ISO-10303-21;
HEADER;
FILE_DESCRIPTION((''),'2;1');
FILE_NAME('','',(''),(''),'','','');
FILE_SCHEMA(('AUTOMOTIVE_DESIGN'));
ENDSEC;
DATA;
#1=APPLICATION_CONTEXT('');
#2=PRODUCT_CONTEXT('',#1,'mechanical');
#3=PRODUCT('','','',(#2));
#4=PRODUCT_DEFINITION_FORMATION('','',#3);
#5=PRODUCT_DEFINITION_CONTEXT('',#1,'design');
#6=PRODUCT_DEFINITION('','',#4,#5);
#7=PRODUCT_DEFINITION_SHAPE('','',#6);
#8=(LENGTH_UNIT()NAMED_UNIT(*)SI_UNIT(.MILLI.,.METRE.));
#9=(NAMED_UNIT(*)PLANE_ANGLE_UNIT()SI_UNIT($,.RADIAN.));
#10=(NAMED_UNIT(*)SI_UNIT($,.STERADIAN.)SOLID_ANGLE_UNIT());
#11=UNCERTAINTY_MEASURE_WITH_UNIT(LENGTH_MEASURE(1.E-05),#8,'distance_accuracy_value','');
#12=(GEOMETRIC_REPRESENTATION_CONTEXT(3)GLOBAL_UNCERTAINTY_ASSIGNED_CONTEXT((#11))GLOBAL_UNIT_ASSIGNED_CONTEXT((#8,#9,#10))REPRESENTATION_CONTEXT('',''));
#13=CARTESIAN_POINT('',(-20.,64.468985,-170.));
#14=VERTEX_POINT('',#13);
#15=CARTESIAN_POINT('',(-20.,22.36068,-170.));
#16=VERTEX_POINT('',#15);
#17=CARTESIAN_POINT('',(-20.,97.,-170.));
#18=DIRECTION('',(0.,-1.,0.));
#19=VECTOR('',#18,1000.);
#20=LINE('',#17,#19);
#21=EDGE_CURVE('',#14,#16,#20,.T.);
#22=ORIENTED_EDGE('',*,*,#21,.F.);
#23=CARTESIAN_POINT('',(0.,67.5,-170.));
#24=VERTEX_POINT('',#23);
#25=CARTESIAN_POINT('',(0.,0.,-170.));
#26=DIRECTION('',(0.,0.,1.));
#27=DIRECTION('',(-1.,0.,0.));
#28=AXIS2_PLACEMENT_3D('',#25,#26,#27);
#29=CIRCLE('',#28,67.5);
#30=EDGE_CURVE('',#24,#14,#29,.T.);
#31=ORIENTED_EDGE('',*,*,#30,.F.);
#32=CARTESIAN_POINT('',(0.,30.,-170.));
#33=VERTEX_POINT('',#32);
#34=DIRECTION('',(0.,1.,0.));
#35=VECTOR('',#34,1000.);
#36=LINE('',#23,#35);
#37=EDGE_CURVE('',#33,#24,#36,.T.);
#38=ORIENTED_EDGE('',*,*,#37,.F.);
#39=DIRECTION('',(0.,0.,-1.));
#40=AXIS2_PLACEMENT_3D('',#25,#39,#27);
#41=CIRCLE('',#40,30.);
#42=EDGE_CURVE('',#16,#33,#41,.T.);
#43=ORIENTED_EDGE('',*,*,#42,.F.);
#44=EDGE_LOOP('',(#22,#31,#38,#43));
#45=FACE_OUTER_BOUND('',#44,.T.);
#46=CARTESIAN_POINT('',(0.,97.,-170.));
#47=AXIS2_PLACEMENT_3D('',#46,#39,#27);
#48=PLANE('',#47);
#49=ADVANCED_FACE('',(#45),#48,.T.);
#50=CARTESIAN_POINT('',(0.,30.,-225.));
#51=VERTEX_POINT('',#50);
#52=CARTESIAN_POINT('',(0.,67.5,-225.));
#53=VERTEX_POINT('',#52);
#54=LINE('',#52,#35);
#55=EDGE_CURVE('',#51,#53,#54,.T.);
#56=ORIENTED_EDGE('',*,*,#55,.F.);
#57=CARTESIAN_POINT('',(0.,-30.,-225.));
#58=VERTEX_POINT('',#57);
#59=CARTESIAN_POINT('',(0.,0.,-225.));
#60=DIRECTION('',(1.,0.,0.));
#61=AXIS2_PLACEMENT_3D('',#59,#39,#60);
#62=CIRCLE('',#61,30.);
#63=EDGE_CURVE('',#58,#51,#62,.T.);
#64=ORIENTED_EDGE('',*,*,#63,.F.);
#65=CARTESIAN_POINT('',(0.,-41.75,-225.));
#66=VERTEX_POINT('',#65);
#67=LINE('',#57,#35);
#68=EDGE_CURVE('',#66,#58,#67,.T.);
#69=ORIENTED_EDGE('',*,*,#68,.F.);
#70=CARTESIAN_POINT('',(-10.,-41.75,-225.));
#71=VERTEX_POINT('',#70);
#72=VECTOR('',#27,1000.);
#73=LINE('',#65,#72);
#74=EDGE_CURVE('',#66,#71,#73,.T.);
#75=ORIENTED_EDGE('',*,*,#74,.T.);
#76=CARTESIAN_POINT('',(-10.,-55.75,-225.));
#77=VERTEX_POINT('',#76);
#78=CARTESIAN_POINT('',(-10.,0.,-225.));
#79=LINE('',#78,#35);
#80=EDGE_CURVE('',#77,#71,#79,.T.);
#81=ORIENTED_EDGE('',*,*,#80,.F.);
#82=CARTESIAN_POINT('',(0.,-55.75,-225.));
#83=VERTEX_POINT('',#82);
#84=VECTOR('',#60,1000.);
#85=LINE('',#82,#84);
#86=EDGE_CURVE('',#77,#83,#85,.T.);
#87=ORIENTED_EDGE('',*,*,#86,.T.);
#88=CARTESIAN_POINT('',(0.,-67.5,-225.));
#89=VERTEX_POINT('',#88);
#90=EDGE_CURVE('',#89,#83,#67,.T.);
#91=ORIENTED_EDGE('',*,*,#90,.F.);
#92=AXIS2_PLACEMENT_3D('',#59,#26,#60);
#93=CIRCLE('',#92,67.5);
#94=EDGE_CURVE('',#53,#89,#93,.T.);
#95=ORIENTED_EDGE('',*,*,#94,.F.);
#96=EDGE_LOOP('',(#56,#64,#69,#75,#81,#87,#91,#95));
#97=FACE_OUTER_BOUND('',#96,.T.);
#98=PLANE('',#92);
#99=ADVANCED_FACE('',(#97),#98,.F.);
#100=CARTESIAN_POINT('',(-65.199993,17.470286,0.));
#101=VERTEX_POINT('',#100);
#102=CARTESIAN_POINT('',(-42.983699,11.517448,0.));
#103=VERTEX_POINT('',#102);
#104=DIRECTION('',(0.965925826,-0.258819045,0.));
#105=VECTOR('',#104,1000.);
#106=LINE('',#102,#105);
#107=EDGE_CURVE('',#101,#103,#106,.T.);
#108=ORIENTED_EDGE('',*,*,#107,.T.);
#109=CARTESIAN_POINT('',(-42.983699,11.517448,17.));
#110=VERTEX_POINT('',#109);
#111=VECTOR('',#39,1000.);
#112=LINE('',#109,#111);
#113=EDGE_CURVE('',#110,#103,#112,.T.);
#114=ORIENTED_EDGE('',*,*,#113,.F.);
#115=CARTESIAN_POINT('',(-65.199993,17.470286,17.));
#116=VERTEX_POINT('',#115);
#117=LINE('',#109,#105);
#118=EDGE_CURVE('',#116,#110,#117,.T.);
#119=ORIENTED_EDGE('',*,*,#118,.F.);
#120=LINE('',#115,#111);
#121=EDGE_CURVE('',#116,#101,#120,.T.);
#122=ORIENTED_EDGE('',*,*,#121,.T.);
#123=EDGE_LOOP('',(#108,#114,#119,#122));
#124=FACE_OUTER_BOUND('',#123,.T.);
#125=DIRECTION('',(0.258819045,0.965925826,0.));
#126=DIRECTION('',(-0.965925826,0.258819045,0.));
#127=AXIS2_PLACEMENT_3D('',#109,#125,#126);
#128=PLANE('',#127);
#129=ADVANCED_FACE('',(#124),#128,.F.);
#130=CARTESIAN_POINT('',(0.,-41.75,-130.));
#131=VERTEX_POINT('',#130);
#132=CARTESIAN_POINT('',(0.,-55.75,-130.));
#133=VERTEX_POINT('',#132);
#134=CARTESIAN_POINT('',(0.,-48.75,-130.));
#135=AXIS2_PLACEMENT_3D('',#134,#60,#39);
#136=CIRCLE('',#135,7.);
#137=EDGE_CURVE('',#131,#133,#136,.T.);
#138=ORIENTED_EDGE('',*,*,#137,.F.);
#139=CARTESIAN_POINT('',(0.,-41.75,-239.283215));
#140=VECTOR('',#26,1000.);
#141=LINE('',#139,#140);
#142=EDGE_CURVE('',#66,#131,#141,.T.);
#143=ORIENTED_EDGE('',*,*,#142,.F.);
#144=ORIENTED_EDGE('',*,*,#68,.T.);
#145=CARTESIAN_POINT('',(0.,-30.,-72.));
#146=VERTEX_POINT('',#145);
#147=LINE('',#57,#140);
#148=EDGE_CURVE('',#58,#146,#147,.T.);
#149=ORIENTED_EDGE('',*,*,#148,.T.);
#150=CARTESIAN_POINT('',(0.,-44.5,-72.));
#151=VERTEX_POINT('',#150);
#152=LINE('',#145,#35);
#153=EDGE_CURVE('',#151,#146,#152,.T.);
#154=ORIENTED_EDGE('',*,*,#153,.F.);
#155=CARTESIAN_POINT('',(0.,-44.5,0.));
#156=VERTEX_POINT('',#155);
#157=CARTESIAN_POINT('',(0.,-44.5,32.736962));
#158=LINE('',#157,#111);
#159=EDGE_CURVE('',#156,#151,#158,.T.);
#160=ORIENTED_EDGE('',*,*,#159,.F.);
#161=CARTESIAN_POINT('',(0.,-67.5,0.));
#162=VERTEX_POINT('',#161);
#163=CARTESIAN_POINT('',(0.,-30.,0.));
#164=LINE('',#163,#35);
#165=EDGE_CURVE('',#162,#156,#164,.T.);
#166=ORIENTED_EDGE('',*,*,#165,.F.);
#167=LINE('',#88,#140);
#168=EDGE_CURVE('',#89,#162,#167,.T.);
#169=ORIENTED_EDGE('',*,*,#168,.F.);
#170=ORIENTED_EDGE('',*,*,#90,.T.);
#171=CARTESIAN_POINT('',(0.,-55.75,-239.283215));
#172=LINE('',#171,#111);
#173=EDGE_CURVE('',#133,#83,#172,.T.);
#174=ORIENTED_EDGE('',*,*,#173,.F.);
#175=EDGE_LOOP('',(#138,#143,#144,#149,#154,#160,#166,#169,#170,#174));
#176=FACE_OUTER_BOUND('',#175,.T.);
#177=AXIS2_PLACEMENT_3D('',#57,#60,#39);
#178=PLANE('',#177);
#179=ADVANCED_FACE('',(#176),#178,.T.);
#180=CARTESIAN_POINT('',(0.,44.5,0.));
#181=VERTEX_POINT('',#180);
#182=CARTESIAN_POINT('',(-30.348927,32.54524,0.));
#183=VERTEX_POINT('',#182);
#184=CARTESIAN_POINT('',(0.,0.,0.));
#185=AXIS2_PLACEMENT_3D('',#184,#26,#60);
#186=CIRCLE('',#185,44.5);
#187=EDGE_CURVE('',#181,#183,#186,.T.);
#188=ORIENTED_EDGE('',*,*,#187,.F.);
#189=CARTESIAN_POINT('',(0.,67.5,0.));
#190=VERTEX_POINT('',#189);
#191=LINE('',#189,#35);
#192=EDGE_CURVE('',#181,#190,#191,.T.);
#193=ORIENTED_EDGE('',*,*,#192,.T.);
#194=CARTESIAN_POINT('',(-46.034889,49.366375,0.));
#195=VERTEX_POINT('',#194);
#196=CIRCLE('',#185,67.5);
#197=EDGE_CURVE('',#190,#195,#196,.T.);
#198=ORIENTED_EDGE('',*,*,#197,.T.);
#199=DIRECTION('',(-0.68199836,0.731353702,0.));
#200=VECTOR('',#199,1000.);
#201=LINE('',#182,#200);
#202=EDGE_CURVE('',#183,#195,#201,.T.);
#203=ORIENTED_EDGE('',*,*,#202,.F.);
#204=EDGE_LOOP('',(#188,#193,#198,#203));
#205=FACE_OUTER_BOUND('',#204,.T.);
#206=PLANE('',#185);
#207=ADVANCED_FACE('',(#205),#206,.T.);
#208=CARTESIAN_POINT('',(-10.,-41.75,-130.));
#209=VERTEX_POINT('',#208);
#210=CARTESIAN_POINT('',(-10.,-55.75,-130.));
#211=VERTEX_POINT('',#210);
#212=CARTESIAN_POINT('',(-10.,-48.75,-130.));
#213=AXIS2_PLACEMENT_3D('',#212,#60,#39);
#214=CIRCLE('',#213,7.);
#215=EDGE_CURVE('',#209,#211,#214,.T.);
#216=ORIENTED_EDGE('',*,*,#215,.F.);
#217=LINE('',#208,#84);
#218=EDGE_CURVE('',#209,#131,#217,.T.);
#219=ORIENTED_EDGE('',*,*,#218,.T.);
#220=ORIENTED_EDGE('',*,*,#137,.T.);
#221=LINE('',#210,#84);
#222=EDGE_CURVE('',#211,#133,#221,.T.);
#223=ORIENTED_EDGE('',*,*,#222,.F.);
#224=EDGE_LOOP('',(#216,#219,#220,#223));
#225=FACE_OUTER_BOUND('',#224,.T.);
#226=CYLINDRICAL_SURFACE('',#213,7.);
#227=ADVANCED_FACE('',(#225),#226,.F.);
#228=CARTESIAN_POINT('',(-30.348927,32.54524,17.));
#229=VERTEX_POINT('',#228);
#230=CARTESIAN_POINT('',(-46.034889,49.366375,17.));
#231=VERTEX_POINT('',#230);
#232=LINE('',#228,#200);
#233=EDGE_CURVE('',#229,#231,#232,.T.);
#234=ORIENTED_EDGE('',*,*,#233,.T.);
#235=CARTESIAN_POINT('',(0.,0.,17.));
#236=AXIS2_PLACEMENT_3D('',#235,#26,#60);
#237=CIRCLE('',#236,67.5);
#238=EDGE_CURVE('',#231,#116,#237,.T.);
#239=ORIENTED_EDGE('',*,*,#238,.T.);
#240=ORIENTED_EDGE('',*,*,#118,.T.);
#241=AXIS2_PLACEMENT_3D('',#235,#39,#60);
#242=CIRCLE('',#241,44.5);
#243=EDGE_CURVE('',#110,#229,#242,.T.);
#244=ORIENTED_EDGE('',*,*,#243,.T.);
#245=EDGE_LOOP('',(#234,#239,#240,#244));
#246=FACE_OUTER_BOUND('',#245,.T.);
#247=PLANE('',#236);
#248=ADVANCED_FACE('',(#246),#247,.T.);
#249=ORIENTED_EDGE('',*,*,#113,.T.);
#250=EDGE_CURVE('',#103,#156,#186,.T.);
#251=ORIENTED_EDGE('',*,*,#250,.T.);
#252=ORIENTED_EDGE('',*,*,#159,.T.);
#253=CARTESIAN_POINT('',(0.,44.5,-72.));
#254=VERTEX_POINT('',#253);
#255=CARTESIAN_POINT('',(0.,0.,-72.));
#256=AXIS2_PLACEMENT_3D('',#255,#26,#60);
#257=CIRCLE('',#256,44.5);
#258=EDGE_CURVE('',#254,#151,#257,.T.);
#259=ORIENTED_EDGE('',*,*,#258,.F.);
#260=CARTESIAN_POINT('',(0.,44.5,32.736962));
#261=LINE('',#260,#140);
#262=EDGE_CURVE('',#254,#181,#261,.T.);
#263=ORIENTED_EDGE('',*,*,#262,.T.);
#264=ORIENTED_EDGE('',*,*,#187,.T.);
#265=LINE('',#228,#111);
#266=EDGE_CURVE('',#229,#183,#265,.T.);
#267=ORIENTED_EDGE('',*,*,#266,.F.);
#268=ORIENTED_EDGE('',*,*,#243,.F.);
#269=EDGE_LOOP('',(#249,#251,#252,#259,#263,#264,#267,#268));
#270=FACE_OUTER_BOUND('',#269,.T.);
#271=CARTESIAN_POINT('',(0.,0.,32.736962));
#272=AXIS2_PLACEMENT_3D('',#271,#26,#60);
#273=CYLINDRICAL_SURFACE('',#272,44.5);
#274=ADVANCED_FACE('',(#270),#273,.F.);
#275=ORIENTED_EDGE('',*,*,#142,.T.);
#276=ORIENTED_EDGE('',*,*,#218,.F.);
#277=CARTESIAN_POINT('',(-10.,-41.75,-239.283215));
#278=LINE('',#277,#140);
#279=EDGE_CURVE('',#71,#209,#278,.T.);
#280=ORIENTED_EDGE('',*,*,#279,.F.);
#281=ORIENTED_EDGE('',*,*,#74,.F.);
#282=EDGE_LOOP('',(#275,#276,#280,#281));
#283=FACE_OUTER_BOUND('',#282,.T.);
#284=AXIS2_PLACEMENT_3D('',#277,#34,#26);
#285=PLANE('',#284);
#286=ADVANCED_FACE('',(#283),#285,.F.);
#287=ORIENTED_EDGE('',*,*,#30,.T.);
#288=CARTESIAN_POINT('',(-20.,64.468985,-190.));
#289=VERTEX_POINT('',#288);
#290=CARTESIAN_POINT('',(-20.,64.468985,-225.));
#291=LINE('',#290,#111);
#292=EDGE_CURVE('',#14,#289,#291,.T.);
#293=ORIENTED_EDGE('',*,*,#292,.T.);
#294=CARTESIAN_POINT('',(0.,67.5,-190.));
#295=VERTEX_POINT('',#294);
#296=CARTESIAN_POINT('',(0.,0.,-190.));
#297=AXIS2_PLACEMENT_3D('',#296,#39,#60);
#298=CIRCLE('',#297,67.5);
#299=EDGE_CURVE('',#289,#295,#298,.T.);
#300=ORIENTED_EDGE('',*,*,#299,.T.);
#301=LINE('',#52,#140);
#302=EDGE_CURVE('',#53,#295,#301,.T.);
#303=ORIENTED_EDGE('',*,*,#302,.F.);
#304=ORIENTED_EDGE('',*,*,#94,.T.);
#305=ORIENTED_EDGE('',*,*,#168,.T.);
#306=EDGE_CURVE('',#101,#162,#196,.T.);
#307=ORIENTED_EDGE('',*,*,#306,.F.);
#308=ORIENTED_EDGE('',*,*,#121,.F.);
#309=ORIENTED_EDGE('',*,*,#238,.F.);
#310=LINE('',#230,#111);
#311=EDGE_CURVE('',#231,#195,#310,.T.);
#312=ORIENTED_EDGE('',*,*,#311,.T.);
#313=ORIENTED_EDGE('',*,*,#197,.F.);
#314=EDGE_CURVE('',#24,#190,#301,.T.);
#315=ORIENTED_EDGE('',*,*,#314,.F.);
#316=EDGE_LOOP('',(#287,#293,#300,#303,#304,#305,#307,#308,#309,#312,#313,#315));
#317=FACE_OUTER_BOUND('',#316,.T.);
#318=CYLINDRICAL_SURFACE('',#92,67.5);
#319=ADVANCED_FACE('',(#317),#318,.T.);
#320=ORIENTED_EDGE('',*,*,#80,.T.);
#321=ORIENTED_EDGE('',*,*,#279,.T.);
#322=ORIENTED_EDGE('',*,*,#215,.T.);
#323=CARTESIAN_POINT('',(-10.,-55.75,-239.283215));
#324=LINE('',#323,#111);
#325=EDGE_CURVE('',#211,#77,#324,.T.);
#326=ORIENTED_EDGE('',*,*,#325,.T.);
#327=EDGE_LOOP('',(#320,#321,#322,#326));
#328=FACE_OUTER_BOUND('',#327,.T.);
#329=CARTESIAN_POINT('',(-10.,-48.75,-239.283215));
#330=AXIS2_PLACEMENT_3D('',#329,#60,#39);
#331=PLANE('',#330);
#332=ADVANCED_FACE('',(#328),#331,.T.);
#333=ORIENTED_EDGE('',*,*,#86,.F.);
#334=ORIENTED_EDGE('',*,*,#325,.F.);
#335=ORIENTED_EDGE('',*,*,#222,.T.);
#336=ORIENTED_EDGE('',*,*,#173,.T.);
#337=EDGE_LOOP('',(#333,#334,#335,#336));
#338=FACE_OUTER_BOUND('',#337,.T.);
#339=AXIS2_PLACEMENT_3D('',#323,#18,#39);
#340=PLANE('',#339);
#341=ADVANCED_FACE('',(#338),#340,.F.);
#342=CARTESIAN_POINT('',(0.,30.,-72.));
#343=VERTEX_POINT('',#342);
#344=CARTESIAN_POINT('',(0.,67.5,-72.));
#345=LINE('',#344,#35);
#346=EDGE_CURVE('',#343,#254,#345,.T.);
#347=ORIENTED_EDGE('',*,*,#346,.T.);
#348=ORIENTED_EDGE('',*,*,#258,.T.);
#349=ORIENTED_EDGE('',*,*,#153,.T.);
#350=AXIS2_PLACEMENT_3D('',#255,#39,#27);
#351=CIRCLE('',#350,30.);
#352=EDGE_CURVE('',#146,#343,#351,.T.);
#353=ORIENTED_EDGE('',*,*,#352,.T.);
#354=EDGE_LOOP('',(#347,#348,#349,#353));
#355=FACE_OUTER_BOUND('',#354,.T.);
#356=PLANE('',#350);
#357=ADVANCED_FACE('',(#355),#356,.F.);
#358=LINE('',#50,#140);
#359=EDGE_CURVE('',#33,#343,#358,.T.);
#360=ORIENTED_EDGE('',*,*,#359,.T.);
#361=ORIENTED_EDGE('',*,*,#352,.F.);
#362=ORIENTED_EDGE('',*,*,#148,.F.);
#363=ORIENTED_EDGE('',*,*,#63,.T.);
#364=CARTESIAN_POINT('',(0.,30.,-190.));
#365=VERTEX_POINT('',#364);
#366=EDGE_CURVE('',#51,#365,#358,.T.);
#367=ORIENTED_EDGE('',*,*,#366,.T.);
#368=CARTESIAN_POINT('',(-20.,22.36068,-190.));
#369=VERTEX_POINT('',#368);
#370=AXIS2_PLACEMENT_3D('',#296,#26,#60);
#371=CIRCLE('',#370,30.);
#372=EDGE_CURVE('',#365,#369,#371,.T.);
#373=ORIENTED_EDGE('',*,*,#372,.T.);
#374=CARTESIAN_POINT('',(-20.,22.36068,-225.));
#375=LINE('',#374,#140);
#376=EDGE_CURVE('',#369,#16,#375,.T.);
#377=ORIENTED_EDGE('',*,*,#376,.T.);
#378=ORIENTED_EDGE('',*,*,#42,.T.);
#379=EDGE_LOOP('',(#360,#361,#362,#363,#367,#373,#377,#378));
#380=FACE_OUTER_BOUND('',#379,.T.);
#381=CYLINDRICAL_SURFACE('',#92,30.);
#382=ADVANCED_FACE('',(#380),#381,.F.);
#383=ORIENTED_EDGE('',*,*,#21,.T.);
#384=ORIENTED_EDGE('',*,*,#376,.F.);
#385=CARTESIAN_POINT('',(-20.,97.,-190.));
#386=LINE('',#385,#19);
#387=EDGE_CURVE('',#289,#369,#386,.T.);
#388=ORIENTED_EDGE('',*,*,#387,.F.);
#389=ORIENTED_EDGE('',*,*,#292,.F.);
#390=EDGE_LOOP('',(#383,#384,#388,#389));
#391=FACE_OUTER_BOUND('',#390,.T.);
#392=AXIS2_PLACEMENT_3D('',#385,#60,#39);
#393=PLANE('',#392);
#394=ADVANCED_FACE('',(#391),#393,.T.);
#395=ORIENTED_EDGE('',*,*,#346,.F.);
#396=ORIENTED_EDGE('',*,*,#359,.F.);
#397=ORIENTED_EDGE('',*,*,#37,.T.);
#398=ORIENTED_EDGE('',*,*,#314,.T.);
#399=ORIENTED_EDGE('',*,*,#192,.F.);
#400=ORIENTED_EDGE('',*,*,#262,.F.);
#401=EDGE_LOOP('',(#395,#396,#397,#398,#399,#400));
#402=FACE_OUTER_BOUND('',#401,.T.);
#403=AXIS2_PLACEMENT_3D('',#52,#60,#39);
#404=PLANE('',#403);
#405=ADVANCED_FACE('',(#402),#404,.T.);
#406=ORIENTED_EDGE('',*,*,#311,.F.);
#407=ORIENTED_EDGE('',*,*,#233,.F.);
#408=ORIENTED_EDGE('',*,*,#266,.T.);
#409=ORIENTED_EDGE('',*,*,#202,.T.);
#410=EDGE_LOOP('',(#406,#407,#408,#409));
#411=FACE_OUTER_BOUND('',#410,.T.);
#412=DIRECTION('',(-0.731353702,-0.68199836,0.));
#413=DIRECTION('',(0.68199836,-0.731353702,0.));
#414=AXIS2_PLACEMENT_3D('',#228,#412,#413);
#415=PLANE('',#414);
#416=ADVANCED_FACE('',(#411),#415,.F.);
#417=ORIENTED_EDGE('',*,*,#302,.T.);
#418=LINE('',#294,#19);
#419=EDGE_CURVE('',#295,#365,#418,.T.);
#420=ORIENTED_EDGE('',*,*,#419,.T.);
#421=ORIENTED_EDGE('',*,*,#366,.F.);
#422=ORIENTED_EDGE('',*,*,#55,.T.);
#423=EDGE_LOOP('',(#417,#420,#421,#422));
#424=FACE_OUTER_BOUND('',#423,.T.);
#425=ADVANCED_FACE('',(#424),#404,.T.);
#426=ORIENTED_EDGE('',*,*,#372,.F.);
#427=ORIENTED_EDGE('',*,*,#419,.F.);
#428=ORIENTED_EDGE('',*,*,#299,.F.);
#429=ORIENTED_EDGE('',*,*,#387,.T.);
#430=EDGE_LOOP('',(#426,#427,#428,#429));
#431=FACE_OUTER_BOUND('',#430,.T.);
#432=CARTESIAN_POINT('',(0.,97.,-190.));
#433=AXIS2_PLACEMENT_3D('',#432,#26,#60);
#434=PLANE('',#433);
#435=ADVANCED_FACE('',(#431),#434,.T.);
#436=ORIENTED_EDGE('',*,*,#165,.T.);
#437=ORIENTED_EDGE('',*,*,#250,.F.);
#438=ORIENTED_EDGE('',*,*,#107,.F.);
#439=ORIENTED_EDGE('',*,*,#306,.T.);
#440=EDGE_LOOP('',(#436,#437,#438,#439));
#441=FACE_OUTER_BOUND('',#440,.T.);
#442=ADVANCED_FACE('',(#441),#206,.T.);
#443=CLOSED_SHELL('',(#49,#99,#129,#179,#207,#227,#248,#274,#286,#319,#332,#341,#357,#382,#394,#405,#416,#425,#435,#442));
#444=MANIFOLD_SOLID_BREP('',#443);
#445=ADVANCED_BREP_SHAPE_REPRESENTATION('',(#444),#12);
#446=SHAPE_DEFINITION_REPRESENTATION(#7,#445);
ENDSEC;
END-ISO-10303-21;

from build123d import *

# Parameters (mm, degrees)
BASE_BLOCK_60X135X225_DEPTH = 225
BORE_PROFILE_SKETCH_W       = 72
BORE_PROFILE_SKETCH_H       = 44.5
SECTOR_START                = 17
SECTOR_BOSS_32DEG_X17_DEPTH = 17
END_NOTCH_SKETCH_W          = 20
END_NOTCH_SKETCH_H          = 20
END_NOTCH_20X35_DEPTH       = 97
SLOT_7X95_DEPTH             = 10


with BuildPart() as part:
    # Base Block Sketch → Base Block 60x135x225 (new body)
    with BuildSketch(Plane.XY):
        with BuildLine():
            Line((0, 67.5), (0, 30))
            ThreePointArc((0, 30), (-30, 0), (0, -30))
            Line((0, -30), (0, -67.5))
            ThreePointArc((0, -67.5), (-67.5, 0), (0, 67.5))
        make_face()
    extrude(amount=-BASE_BLOCK_60X135X225_DEPTH)

    # Bore Profile Sketch → Bore Revolve Cut (revolve, cut)
    with BuildSketch(Plane(origin=(0, 0, 0), x_dir=(0, 0, -1), z_dir=(1, 0, 0))):
        with Locations((36, 22.25)):
            Rectangle(BORE_PROFILE_SKETCH_W, BORE_PROFILE_SKETCH_H)
    revolve(axis=Axis((0, 0, 32.736961991), (0, 0, -1)), mode=Mode.SUBTRACT)

    # Sector Boss Sketch → Sector Boss 32deg x17 (add)
    with BuildSketch(Plane.XY.offset(SECTOR_START)):
        with BuildLine():
            Line((-30.348927023, 32.545239722), (-46.034889304, 49.366374859))
            ThreePointArc((-46.034889304, 49.366374859), (-57.858792797, 34.765070056), (-65.199993275, 17.470285544))
            Line((-65.199993275, 17.470285544), (-42.98369927, 11.517447507))
            ThreePointArc((-42.98369927, 11.517447507), (-38.143944881, 22.919194333), (-30.348927023, 32.545239722))
        make_face()
    extrude(amount=-SECTOR_BOSS_32DEG_X17_DEPTH)

    # End Notch Sketch → End Notch 20x35 (cut)
    with BuildSketch(Plane(origin=(0, 0, 0), x_dir=(1, 0, 0), z_dir=(0, 1, 0))):
        with Locations((-10, 180)):
            Rectangle(END_NOTCH_SKETCH_W, END_NOTCH_SKETCH_H)
    extrude(amount=END_NOTCH_20X35_DEPTH, mode=Mode.SUBTRACT)

    # Slot Sketch → Slot 7x95 (cut)
    with BuildSketch(Plane(origin=(0, 0, 0), x_dir=(0, 0, -1), z_dir=(1, 0, 0))):
        with BuildLine():
            Line((239.283215377, -55.75), (130, -55.75))
            ThreePointArc((130, -55.75), (123, -48.75), (130, -41.75))
            Line((130, -41.75), (239.283215377, -41.75))
            ThreePointArc((239.283215377, -41.75), (246.283215377, -48.75), (239.283215377, -55.75))
        make_face()
    extrude(amount=-SLOT_7X95_DEPTH, mode=Mode.SUBTRACT)


solid = part.part
